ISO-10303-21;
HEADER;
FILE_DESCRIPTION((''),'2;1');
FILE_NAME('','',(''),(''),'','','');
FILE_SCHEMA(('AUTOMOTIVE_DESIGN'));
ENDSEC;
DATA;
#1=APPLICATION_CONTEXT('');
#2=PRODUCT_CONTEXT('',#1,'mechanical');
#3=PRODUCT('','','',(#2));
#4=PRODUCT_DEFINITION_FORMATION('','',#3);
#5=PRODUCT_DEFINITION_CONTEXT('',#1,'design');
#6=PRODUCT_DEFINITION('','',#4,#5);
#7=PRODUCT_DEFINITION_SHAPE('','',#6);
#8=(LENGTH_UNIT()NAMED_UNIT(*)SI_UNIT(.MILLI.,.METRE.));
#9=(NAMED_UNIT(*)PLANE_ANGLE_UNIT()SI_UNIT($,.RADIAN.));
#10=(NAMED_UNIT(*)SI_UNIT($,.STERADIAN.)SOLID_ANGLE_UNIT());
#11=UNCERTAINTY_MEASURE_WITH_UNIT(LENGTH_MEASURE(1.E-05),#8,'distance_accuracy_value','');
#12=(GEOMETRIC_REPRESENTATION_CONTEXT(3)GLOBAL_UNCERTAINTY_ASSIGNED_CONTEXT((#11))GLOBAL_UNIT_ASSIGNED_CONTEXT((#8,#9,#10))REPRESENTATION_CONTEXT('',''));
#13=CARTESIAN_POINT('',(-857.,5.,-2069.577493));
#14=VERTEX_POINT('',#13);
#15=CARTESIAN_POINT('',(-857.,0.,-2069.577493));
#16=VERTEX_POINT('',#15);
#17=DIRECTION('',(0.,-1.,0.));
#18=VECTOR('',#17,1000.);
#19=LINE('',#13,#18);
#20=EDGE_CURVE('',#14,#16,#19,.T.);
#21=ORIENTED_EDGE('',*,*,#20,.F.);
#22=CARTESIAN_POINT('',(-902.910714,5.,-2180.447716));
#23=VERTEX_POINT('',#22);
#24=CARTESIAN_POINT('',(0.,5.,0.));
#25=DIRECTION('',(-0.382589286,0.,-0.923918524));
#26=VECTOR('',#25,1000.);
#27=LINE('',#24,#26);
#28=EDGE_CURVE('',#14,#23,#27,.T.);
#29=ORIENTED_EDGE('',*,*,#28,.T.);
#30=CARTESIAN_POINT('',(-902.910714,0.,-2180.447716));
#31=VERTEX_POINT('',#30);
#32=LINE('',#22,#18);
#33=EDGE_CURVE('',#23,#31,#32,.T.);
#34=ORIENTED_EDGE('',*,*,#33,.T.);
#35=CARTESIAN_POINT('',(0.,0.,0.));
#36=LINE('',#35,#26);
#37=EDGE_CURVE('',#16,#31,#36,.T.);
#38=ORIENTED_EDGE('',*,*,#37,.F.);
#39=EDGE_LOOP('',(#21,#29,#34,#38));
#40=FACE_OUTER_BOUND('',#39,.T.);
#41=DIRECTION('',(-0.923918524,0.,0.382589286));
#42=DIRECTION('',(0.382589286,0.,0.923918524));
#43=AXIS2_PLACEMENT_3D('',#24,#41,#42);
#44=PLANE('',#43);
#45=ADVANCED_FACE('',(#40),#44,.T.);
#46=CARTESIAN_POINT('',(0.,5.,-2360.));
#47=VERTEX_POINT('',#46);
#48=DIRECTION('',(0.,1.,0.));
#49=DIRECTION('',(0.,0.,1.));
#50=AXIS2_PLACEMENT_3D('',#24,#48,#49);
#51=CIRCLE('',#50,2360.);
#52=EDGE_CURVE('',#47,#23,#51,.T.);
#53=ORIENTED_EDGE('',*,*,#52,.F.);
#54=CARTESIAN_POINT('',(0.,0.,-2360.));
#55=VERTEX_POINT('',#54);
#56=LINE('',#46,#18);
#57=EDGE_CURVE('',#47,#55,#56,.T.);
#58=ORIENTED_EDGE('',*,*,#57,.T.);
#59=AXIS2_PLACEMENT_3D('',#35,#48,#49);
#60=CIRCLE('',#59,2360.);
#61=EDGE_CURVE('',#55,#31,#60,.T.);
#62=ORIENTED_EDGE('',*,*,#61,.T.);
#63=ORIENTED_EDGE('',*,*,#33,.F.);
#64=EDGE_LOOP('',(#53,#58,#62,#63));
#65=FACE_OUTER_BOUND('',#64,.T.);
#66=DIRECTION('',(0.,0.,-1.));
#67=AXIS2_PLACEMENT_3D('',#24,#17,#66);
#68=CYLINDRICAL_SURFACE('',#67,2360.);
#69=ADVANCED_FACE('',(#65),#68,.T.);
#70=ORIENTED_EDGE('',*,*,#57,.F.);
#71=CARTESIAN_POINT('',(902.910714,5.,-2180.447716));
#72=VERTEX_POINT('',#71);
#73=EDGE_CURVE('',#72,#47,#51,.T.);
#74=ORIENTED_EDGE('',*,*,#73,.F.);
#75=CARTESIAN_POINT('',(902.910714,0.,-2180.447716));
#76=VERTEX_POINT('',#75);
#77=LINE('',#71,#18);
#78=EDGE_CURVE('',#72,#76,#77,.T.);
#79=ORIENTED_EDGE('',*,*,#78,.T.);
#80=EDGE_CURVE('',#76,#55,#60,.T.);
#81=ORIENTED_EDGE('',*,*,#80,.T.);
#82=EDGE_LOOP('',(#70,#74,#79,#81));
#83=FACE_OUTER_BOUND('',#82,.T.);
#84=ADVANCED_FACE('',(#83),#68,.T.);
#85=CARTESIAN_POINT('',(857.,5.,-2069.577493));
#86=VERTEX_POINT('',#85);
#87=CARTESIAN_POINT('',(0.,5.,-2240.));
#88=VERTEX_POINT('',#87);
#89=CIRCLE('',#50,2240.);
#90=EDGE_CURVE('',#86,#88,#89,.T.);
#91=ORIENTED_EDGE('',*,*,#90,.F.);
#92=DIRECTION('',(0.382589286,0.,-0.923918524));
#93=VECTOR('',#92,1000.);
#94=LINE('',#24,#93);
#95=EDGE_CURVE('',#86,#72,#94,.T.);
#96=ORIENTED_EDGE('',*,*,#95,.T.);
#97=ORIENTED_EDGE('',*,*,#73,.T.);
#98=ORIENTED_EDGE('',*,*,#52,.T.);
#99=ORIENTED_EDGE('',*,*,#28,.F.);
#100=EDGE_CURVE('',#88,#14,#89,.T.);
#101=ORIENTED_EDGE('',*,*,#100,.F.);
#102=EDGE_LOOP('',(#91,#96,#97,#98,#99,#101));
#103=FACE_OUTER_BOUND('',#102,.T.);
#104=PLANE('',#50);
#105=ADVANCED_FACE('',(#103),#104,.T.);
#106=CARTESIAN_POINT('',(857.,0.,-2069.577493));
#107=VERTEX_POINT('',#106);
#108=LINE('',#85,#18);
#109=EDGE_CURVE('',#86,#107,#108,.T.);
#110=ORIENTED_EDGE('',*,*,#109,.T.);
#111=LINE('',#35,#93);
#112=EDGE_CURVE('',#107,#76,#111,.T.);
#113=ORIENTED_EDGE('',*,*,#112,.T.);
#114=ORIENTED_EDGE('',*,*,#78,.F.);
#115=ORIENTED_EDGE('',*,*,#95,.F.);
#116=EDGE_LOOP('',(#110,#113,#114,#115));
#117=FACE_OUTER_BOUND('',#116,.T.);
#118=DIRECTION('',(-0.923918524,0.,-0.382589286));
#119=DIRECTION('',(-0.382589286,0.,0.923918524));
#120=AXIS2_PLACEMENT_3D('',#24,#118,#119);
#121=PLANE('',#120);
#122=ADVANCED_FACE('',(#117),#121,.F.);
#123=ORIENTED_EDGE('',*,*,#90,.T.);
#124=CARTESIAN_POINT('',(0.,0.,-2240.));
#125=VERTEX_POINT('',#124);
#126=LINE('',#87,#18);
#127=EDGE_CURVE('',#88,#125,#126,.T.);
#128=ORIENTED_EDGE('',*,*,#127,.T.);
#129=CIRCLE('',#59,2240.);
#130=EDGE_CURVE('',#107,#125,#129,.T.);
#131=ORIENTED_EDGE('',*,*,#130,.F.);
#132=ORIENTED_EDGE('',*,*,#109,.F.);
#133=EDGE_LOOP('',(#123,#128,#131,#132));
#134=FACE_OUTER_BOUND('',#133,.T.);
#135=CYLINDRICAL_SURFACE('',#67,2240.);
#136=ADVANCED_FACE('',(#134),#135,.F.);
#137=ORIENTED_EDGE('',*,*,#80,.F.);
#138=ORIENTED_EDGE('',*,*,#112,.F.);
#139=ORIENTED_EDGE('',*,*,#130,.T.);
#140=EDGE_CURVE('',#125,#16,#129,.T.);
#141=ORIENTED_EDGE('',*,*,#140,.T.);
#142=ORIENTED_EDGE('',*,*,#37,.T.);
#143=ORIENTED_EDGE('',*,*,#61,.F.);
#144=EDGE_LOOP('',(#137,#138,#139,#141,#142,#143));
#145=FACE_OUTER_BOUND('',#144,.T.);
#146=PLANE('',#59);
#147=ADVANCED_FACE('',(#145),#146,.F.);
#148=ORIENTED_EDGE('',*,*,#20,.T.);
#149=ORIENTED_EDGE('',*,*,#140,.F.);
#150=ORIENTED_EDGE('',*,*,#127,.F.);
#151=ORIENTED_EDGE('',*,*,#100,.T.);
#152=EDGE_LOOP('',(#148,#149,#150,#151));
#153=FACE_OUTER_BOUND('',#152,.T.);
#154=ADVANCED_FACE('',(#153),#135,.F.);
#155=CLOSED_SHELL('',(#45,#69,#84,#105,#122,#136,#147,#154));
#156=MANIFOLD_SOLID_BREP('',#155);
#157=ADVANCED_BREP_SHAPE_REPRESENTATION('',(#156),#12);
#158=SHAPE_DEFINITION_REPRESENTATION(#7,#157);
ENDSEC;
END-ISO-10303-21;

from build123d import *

# Parameters (mm, degrees)
BOSS_EXTRUDE1_DEPTH = 5


with BuildPart() as part:
    # Sketch2 → Boss-Extrude1 (new body)
    with BuildSketch(Plane(origin=(0, 0, 0), x_dir=(1, 0, 0), z_dir=(0, 1, 0))):
        with BuildLine():
            Line((-902.910714286, 2180.447715958), (-857, 2069.577493113))
            ThreePointArc((-857, 2069.577493113), (0, 2240), (857, 2069.577493113))
            Line((857, 2069.577493113), (902.910714286, 2180.447715958))
            ThreePointArc((902.910714286, 2180.447715958), (0, 2360), (-902.910714286, 2180.447715958))
        make_face()
    extrude(amount=BOSS_EXTRUDE1_DEPTH)


solid = part.part
